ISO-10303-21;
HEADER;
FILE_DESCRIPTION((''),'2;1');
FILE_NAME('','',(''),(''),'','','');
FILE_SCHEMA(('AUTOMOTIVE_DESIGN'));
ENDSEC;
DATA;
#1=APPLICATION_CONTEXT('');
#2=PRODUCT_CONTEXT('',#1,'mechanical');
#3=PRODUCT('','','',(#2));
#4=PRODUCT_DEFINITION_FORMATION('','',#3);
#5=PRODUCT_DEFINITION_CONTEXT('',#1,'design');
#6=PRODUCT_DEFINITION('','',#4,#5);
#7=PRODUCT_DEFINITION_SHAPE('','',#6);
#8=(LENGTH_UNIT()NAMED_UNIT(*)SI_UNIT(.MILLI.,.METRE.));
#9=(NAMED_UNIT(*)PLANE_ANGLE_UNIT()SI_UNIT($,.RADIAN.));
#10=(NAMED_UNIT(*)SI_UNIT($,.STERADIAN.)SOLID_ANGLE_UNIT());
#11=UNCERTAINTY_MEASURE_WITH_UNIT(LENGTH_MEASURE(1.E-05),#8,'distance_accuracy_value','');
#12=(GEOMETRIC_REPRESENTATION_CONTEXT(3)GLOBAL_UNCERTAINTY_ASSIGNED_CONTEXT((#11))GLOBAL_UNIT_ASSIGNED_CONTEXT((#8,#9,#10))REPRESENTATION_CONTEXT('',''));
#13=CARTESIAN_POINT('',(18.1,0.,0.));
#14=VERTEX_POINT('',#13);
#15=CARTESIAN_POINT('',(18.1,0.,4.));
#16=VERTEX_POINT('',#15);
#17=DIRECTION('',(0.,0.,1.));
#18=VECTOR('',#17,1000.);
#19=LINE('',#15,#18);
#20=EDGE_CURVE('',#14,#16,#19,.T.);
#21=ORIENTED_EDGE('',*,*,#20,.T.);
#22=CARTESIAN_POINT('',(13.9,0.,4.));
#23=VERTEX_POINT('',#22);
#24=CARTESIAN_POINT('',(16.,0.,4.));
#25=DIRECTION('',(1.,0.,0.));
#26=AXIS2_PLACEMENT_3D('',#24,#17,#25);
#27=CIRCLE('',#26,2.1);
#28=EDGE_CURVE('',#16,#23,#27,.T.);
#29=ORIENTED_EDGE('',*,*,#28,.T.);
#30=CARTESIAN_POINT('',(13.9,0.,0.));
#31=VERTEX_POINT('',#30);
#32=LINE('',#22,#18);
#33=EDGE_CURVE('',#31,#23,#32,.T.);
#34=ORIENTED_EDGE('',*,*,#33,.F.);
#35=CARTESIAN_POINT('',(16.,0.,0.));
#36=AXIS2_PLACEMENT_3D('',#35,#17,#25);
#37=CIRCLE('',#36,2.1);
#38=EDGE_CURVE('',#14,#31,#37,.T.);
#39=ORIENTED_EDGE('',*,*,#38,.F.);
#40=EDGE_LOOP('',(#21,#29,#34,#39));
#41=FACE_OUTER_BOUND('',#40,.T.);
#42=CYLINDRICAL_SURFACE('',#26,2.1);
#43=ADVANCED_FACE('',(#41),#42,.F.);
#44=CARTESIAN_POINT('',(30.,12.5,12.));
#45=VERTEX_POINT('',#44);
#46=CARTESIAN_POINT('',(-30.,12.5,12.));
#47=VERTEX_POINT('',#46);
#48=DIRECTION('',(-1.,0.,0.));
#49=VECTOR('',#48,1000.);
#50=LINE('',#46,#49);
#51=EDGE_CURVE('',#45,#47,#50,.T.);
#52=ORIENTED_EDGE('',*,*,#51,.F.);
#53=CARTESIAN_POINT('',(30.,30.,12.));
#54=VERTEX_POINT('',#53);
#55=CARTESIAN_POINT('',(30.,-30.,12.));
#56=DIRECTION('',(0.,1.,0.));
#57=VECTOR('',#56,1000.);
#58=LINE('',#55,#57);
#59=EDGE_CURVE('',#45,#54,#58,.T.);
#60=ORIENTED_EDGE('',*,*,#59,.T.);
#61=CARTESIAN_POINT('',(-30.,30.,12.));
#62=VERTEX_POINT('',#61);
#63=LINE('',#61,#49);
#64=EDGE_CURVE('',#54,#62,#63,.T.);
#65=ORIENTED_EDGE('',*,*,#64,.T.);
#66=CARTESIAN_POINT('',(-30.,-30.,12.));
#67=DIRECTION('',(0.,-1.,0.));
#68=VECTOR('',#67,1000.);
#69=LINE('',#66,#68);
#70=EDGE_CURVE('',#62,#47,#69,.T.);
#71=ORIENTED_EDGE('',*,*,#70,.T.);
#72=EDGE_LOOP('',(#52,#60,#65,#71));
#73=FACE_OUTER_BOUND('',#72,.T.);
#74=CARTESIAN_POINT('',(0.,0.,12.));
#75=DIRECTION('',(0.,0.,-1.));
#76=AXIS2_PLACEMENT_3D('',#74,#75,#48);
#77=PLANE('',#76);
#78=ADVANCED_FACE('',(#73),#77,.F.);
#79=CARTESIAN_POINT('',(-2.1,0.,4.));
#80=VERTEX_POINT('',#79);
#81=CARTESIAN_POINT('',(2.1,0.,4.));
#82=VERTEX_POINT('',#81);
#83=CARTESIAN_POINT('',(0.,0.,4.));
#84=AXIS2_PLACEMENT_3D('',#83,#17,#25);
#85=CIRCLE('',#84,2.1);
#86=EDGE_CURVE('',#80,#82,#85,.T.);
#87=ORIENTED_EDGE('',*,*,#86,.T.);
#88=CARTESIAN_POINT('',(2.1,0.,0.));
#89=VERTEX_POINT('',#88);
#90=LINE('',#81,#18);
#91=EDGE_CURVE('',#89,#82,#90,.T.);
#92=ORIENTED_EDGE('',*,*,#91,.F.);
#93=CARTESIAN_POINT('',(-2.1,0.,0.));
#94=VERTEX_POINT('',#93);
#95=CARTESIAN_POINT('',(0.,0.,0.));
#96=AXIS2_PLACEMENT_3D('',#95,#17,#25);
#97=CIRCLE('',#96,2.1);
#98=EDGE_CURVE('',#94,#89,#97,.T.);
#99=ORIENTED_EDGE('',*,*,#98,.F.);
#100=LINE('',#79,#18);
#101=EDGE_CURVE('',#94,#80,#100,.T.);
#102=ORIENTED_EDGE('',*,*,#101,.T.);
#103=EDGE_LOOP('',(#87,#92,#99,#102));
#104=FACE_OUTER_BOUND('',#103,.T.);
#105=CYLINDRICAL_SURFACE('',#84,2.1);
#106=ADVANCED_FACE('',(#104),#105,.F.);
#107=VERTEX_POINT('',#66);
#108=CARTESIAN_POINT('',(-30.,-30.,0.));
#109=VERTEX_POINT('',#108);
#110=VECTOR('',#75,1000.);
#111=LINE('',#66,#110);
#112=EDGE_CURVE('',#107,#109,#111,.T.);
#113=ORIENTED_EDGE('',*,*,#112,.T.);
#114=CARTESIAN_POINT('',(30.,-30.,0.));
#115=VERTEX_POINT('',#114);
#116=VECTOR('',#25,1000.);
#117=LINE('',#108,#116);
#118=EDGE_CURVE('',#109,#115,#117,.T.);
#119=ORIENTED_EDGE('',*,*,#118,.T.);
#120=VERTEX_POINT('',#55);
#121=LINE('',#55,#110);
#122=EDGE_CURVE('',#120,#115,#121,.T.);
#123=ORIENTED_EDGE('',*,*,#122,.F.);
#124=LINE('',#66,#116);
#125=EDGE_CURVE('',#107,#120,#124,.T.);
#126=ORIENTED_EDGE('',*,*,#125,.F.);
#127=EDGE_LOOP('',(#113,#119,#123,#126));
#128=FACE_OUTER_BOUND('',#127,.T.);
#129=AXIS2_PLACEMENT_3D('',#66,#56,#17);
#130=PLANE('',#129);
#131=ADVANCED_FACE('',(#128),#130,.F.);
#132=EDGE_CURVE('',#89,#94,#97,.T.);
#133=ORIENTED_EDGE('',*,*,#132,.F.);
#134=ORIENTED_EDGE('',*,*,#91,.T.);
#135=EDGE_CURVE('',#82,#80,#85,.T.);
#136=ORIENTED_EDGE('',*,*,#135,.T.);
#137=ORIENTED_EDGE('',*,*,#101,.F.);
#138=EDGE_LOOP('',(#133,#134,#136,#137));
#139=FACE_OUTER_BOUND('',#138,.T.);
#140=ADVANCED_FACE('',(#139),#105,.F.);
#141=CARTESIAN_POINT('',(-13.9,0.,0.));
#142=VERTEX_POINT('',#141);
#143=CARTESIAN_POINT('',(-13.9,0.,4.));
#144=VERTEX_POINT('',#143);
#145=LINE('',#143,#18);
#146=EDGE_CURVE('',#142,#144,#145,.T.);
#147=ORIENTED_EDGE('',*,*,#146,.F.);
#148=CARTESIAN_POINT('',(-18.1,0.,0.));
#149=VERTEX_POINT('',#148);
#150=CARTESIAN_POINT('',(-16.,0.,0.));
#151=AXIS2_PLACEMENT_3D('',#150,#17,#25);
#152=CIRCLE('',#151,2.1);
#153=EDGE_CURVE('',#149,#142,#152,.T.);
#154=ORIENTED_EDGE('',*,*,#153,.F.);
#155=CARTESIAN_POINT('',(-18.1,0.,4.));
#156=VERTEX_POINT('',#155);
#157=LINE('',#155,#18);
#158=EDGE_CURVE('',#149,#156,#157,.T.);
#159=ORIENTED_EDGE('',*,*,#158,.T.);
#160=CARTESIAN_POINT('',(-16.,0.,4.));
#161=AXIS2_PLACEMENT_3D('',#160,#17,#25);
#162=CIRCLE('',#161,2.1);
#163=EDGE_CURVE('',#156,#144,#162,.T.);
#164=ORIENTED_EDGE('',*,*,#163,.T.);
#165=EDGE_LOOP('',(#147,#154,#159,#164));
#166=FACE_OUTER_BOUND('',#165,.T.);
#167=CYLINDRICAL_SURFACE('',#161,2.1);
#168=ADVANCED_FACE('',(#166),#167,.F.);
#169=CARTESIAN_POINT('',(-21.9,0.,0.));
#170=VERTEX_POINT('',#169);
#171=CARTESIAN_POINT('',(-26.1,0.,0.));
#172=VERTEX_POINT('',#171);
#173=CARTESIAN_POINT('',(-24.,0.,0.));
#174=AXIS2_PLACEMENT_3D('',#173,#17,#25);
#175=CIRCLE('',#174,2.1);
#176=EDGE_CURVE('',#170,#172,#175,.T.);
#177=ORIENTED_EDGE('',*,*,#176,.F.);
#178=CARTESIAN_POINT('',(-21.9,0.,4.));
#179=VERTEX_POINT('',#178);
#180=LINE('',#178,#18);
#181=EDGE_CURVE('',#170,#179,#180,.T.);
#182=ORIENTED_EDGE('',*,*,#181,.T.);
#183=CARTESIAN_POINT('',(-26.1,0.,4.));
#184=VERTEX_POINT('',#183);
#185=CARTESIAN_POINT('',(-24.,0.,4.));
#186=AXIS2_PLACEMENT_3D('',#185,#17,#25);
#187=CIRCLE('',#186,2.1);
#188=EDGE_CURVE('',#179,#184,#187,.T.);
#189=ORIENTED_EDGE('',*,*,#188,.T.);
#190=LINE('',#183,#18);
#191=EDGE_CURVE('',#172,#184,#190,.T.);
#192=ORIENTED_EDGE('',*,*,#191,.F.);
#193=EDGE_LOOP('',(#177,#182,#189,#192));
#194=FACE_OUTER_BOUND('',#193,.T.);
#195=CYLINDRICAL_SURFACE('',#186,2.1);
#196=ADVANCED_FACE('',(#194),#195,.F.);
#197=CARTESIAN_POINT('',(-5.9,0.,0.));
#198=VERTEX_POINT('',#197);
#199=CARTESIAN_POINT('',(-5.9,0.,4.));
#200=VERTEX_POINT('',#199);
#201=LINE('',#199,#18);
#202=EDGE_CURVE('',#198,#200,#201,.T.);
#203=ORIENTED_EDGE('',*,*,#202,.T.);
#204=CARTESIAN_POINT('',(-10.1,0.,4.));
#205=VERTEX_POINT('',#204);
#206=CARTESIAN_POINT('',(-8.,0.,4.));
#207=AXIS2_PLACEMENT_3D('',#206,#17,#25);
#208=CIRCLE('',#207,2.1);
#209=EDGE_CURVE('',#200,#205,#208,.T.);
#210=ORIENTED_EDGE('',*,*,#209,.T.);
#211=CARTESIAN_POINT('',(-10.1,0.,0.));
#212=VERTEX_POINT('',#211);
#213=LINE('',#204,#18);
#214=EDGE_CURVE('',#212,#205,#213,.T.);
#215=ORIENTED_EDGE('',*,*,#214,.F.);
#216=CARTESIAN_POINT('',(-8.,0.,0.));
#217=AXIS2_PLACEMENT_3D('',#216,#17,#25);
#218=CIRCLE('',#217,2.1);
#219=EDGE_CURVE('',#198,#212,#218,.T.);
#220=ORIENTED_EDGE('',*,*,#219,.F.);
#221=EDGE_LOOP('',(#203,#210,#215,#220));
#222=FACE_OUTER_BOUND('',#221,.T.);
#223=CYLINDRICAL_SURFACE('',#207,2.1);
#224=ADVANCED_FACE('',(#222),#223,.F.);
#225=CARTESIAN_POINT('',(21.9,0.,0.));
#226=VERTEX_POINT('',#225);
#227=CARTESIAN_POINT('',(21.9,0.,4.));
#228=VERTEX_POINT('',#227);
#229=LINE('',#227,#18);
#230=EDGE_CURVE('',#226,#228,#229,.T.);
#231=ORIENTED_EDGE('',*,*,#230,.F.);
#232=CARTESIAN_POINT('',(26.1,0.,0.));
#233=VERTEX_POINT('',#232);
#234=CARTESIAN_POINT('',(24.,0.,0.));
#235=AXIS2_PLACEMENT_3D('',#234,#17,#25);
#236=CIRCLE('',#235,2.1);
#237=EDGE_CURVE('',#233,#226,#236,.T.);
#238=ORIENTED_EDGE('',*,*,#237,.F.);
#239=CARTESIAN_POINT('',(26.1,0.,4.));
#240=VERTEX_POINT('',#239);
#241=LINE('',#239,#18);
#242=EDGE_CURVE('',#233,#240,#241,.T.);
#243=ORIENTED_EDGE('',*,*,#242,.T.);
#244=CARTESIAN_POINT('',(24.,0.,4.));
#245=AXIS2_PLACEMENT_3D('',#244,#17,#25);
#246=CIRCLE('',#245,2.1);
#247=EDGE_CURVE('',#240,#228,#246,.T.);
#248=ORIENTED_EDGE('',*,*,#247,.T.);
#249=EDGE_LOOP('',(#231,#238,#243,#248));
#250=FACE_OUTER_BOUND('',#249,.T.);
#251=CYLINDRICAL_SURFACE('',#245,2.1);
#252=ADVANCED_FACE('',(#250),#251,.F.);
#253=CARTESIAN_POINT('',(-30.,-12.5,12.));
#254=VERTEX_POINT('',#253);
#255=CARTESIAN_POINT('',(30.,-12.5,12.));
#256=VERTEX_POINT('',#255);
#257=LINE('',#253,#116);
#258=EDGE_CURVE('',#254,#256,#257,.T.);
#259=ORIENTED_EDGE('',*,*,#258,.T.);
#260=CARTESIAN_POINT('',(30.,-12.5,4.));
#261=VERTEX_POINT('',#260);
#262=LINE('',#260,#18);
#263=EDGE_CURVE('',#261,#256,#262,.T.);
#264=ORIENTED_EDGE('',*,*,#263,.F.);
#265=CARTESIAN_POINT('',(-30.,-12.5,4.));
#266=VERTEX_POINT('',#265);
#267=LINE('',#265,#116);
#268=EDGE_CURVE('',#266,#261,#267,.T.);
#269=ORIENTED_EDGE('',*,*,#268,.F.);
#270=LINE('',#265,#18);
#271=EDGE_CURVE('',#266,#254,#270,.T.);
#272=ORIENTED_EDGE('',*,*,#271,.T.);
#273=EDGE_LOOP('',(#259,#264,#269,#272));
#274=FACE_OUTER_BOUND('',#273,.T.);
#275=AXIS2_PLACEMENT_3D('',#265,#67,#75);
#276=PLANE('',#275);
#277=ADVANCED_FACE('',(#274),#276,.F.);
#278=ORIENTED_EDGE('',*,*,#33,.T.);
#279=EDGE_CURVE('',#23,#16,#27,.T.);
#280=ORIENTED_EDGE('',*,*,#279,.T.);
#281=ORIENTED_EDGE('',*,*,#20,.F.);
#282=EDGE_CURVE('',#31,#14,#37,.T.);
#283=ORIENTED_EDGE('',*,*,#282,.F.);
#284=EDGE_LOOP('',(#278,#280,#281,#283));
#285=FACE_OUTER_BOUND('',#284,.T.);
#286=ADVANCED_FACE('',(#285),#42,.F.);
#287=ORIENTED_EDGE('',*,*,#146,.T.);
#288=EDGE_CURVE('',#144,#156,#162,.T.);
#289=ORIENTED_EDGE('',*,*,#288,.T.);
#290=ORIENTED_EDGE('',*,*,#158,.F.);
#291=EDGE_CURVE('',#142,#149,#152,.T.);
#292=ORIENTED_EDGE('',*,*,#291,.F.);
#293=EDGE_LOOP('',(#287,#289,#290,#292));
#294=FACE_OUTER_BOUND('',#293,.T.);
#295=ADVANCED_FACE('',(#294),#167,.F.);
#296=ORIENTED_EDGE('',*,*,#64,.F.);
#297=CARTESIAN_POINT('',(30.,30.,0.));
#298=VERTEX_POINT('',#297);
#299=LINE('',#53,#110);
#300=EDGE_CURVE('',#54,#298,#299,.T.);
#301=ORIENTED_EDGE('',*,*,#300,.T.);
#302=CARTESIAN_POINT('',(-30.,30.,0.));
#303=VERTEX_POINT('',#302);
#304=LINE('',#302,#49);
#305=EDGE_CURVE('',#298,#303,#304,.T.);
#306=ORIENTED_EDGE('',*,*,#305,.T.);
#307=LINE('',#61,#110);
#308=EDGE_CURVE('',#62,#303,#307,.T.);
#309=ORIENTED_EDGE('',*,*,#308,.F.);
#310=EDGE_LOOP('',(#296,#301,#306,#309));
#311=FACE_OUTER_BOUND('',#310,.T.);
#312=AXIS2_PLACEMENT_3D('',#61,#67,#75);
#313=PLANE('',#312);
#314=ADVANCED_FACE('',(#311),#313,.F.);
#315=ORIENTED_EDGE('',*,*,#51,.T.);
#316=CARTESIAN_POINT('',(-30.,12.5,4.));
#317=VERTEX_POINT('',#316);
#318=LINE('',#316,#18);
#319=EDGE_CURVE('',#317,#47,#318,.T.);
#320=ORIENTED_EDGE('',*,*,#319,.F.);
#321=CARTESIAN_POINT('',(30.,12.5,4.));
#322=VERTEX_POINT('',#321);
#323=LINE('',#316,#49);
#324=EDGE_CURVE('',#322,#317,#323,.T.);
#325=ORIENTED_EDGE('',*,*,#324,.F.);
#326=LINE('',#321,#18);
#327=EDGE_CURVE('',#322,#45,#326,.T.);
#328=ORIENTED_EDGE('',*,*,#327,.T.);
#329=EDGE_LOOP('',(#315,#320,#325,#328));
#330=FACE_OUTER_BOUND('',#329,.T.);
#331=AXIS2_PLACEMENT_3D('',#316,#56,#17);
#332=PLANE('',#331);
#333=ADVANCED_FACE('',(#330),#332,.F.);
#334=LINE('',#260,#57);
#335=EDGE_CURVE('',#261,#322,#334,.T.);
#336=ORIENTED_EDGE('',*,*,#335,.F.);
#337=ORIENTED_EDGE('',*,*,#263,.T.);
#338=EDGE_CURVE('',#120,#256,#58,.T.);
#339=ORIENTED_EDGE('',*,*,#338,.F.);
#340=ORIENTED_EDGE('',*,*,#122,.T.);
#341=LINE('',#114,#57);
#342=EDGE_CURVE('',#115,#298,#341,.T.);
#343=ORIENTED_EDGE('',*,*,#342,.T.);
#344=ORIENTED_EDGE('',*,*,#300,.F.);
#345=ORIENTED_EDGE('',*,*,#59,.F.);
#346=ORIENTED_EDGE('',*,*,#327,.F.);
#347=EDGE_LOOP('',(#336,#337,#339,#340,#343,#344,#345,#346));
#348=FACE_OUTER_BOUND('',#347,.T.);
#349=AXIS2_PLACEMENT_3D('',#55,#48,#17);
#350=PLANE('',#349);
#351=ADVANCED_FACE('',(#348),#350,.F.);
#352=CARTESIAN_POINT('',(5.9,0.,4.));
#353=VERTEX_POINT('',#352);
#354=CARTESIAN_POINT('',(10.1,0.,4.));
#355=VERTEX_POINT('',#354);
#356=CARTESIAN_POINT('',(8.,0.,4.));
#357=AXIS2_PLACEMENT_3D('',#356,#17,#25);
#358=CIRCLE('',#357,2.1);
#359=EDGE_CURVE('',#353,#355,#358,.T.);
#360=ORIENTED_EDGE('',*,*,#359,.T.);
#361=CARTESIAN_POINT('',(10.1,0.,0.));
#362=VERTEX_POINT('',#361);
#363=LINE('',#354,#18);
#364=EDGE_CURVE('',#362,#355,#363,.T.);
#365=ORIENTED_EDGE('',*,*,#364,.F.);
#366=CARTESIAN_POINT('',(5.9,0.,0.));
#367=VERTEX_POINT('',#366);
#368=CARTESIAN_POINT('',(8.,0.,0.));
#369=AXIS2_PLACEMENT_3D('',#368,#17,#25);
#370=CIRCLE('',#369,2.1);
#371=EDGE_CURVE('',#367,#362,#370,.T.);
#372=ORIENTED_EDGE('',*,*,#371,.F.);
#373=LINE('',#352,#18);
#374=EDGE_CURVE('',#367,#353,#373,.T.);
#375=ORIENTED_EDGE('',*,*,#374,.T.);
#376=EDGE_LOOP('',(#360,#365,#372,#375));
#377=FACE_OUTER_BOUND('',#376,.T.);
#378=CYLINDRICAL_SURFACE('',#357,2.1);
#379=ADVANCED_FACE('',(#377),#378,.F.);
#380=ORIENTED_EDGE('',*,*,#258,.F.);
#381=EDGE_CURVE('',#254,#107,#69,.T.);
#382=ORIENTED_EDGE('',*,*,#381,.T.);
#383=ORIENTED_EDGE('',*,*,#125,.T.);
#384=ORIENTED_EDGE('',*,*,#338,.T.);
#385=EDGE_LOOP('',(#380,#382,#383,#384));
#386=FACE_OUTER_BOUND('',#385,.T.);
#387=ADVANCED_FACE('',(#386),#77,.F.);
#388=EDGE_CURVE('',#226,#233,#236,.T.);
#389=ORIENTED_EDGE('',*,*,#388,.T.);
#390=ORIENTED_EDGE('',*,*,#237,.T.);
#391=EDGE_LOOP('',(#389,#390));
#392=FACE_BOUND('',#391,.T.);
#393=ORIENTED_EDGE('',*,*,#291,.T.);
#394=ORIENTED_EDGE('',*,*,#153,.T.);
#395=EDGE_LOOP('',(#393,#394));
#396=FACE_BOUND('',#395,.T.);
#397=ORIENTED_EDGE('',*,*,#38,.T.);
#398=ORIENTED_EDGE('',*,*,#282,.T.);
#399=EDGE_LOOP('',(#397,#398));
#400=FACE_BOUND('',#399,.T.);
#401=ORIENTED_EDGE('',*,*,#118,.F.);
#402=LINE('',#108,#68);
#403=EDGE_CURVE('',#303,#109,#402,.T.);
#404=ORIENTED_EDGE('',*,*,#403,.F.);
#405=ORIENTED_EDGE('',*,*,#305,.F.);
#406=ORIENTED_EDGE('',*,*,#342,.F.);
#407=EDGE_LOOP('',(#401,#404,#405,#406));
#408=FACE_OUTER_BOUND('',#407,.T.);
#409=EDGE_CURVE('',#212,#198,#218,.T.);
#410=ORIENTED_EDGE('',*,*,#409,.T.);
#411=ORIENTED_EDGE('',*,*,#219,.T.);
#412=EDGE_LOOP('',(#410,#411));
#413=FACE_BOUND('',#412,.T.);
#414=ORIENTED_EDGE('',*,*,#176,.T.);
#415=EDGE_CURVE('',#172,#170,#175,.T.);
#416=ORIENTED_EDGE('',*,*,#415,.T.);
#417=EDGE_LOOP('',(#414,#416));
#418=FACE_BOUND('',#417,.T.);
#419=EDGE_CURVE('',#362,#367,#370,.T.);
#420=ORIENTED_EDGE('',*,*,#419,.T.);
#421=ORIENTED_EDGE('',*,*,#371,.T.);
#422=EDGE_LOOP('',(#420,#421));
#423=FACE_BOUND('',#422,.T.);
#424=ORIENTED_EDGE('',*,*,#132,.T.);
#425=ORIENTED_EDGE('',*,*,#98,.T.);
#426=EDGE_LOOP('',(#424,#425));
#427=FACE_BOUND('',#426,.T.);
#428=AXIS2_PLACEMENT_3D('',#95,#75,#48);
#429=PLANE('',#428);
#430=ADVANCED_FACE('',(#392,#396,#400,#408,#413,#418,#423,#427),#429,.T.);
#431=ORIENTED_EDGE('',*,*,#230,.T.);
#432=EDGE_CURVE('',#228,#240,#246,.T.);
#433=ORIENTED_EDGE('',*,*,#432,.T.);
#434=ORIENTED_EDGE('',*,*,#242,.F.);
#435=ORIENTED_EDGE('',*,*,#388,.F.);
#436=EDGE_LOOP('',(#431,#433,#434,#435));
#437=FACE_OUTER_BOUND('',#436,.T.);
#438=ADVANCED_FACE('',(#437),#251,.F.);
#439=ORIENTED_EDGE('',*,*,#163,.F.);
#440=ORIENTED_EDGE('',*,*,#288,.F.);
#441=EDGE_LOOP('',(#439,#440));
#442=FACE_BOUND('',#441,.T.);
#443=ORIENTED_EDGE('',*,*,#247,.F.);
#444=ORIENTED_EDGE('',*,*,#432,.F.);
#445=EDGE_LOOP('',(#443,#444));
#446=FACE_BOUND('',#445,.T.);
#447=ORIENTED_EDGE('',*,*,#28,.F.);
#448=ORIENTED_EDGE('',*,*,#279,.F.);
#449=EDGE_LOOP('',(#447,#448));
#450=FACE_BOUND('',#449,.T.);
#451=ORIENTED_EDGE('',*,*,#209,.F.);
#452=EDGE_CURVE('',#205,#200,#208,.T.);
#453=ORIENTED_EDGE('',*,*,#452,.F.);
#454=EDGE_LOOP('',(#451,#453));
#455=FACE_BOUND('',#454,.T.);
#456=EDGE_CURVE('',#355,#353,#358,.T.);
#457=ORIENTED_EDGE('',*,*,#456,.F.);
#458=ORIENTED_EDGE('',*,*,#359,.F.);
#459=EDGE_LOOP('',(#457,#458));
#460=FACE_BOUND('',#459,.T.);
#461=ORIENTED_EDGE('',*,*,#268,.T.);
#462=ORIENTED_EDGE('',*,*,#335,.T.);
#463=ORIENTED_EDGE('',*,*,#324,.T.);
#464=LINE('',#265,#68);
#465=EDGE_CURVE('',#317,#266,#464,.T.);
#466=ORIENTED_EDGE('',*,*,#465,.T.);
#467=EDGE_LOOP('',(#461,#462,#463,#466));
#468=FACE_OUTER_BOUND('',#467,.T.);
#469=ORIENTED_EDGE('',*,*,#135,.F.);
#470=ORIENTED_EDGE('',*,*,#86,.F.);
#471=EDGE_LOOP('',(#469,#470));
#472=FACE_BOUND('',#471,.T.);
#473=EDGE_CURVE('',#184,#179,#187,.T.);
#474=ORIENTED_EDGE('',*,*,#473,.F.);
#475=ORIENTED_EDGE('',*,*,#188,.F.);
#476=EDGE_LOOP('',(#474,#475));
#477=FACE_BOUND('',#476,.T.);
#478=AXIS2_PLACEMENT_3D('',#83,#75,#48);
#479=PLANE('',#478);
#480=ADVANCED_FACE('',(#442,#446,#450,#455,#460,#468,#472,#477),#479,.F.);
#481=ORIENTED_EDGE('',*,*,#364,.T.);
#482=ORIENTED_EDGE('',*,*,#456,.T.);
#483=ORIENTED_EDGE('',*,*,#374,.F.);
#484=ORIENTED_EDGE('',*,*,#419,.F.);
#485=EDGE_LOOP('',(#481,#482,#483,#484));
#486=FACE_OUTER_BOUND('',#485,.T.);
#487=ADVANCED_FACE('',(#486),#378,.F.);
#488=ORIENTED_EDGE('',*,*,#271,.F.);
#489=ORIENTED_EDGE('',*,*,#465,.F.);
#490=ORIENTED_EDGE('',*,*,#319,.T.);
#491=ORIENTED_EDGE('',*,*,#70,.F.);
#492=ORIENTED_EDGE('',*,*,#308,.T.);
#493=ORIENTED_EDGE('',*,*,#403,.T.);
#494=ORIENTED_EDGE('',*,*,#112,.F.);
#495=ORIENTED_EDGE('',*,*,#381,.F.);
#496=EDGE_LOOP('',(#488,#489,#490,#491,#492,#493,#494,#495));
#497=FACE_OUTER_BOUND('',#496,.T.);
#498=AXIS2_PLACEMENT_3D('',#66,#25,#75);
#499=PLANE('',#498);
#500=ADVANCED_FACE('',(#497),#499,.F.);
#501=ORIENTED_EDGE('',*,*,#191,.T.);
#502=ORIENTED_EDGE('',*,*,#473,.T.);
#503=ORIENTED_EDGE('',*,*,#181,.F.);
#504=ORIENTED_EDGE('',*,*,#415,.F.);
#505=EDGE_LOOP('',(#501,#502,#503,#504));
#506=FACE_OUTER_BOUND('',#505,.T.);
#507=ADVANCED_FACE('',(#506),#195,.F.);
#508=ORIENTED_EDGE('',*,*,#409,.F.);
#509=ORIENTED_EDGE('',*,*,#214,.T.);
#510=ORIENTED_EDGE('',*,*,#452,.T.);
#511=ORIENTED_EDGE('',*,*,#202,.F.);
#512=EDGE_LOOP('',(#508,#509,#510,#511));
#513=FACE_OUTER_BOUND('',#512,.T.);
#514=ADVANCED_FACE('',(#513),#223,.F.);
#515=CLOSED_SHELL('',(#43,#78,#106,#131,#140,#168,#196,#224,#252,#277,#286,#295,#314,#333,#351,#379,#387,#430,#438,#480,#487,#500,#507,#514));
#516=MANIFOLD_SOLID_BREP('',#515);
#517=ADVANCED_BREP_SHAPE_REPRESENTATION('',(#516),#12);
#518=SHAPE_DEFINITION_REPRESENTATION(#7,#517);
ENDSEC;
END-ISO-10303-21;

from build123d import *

# Parameters (mm, degrees)
SKETCH_1_W             = 60
SKETCH_1_H             = 60
EXTRUDE_1_DEPTH        = 12
SKETCH_2_W             = 60
SKETCH_2_H             = 25
CUT_EXTRUDE_1_DEPTH    = 8
HOLE_WIZARD_M5_1_D     = 4.2
PATTERN_LINEAR_1_COUNT = 4
PATTERN_LINEAR_1_PITCH = 8
MIRROR_1_COPY_1_D      = 4.2
MIRROR_1_COPY_2_D      = 4.2
MIRROR_1_COPY_3_D      = 4.2
MIRROR_1_COPY_4_D      = 4.2


with BuildPart() as part:
    # 草图1 → 凸台-拉伸1 (new body)
    with BuildSketch(Plane.XY):
        Rectangle(SKETCH_1_W, SKETCH_1_H)
    extrude(amount=EXTRUDE_1_DEPTH)

    # 草图2 → 切除-拉伸1 (cut)
    with BuildSketch(Plane.XY.offset(12)):
        Rectangle(SKETCH_2_W, SKETCH_2_H)
    extrude(amount=-CUT_EXTRUDE_1_DEPTH, mode=Mode.SUBTRACT)

    # M5 螺纹孔1 (through all)
    with Locations(Plane.XY.offset(4)):
        with Locations((0, 0)):
            hole_wizard_m5_1 = Hole(HOLE_WIZARD_M5_1_D / 2)

    # 阵列(线性)1: M5 螺纹孔1 ×4
    with Locations(*[(-i * PATTERN_LINEAR_1_PITCH, 0, 0) for i in range(1, PATTERN_LINEAR_1_COUNT)]):
        add(hole_wizard_m5_1, mode=Mode.SUBTRACT)

    # 镜向1 copy 1 (through all)
    with Locations(Plane(origin=(8, 0, 4), x_dir=(-1, 0, 0), z_dir=(0, 0, 1))):
        with Locations((0, 0)):
            Hole(MIRROR_1_COPY_1_D / 2)

    # 镜向1 copy 2 (through all)
    with Locations(Plane(origin=(16, 0, 4), x_dir=(-1, 0, 0), z_dir=(0, 0, 1))):
        with Locations((0, 0)):
            Hole(MIRROR_1_COPY_2_D / 2)

    # 镜向1 copy 3 (through all)
    with Locations(Plane(origin=(24, 0, 4), x_dir=(-1, 0, 0), z_dir=(0, 0, 1))):
        with Locations((0, 0)):
            Hole(MIRROR_1_COPY_3_D / 2)

    # 镜向1 copy 4 (through all)
    with Locations(Plane(origin=(0, 0, 4), x_dir=(-1, 0, 0), z_dir=(0, 0, 1))):
        with Locations((0, 0)):
            Hole(MIRROR_1_COPY_4_D / 2)


solid = part.part
